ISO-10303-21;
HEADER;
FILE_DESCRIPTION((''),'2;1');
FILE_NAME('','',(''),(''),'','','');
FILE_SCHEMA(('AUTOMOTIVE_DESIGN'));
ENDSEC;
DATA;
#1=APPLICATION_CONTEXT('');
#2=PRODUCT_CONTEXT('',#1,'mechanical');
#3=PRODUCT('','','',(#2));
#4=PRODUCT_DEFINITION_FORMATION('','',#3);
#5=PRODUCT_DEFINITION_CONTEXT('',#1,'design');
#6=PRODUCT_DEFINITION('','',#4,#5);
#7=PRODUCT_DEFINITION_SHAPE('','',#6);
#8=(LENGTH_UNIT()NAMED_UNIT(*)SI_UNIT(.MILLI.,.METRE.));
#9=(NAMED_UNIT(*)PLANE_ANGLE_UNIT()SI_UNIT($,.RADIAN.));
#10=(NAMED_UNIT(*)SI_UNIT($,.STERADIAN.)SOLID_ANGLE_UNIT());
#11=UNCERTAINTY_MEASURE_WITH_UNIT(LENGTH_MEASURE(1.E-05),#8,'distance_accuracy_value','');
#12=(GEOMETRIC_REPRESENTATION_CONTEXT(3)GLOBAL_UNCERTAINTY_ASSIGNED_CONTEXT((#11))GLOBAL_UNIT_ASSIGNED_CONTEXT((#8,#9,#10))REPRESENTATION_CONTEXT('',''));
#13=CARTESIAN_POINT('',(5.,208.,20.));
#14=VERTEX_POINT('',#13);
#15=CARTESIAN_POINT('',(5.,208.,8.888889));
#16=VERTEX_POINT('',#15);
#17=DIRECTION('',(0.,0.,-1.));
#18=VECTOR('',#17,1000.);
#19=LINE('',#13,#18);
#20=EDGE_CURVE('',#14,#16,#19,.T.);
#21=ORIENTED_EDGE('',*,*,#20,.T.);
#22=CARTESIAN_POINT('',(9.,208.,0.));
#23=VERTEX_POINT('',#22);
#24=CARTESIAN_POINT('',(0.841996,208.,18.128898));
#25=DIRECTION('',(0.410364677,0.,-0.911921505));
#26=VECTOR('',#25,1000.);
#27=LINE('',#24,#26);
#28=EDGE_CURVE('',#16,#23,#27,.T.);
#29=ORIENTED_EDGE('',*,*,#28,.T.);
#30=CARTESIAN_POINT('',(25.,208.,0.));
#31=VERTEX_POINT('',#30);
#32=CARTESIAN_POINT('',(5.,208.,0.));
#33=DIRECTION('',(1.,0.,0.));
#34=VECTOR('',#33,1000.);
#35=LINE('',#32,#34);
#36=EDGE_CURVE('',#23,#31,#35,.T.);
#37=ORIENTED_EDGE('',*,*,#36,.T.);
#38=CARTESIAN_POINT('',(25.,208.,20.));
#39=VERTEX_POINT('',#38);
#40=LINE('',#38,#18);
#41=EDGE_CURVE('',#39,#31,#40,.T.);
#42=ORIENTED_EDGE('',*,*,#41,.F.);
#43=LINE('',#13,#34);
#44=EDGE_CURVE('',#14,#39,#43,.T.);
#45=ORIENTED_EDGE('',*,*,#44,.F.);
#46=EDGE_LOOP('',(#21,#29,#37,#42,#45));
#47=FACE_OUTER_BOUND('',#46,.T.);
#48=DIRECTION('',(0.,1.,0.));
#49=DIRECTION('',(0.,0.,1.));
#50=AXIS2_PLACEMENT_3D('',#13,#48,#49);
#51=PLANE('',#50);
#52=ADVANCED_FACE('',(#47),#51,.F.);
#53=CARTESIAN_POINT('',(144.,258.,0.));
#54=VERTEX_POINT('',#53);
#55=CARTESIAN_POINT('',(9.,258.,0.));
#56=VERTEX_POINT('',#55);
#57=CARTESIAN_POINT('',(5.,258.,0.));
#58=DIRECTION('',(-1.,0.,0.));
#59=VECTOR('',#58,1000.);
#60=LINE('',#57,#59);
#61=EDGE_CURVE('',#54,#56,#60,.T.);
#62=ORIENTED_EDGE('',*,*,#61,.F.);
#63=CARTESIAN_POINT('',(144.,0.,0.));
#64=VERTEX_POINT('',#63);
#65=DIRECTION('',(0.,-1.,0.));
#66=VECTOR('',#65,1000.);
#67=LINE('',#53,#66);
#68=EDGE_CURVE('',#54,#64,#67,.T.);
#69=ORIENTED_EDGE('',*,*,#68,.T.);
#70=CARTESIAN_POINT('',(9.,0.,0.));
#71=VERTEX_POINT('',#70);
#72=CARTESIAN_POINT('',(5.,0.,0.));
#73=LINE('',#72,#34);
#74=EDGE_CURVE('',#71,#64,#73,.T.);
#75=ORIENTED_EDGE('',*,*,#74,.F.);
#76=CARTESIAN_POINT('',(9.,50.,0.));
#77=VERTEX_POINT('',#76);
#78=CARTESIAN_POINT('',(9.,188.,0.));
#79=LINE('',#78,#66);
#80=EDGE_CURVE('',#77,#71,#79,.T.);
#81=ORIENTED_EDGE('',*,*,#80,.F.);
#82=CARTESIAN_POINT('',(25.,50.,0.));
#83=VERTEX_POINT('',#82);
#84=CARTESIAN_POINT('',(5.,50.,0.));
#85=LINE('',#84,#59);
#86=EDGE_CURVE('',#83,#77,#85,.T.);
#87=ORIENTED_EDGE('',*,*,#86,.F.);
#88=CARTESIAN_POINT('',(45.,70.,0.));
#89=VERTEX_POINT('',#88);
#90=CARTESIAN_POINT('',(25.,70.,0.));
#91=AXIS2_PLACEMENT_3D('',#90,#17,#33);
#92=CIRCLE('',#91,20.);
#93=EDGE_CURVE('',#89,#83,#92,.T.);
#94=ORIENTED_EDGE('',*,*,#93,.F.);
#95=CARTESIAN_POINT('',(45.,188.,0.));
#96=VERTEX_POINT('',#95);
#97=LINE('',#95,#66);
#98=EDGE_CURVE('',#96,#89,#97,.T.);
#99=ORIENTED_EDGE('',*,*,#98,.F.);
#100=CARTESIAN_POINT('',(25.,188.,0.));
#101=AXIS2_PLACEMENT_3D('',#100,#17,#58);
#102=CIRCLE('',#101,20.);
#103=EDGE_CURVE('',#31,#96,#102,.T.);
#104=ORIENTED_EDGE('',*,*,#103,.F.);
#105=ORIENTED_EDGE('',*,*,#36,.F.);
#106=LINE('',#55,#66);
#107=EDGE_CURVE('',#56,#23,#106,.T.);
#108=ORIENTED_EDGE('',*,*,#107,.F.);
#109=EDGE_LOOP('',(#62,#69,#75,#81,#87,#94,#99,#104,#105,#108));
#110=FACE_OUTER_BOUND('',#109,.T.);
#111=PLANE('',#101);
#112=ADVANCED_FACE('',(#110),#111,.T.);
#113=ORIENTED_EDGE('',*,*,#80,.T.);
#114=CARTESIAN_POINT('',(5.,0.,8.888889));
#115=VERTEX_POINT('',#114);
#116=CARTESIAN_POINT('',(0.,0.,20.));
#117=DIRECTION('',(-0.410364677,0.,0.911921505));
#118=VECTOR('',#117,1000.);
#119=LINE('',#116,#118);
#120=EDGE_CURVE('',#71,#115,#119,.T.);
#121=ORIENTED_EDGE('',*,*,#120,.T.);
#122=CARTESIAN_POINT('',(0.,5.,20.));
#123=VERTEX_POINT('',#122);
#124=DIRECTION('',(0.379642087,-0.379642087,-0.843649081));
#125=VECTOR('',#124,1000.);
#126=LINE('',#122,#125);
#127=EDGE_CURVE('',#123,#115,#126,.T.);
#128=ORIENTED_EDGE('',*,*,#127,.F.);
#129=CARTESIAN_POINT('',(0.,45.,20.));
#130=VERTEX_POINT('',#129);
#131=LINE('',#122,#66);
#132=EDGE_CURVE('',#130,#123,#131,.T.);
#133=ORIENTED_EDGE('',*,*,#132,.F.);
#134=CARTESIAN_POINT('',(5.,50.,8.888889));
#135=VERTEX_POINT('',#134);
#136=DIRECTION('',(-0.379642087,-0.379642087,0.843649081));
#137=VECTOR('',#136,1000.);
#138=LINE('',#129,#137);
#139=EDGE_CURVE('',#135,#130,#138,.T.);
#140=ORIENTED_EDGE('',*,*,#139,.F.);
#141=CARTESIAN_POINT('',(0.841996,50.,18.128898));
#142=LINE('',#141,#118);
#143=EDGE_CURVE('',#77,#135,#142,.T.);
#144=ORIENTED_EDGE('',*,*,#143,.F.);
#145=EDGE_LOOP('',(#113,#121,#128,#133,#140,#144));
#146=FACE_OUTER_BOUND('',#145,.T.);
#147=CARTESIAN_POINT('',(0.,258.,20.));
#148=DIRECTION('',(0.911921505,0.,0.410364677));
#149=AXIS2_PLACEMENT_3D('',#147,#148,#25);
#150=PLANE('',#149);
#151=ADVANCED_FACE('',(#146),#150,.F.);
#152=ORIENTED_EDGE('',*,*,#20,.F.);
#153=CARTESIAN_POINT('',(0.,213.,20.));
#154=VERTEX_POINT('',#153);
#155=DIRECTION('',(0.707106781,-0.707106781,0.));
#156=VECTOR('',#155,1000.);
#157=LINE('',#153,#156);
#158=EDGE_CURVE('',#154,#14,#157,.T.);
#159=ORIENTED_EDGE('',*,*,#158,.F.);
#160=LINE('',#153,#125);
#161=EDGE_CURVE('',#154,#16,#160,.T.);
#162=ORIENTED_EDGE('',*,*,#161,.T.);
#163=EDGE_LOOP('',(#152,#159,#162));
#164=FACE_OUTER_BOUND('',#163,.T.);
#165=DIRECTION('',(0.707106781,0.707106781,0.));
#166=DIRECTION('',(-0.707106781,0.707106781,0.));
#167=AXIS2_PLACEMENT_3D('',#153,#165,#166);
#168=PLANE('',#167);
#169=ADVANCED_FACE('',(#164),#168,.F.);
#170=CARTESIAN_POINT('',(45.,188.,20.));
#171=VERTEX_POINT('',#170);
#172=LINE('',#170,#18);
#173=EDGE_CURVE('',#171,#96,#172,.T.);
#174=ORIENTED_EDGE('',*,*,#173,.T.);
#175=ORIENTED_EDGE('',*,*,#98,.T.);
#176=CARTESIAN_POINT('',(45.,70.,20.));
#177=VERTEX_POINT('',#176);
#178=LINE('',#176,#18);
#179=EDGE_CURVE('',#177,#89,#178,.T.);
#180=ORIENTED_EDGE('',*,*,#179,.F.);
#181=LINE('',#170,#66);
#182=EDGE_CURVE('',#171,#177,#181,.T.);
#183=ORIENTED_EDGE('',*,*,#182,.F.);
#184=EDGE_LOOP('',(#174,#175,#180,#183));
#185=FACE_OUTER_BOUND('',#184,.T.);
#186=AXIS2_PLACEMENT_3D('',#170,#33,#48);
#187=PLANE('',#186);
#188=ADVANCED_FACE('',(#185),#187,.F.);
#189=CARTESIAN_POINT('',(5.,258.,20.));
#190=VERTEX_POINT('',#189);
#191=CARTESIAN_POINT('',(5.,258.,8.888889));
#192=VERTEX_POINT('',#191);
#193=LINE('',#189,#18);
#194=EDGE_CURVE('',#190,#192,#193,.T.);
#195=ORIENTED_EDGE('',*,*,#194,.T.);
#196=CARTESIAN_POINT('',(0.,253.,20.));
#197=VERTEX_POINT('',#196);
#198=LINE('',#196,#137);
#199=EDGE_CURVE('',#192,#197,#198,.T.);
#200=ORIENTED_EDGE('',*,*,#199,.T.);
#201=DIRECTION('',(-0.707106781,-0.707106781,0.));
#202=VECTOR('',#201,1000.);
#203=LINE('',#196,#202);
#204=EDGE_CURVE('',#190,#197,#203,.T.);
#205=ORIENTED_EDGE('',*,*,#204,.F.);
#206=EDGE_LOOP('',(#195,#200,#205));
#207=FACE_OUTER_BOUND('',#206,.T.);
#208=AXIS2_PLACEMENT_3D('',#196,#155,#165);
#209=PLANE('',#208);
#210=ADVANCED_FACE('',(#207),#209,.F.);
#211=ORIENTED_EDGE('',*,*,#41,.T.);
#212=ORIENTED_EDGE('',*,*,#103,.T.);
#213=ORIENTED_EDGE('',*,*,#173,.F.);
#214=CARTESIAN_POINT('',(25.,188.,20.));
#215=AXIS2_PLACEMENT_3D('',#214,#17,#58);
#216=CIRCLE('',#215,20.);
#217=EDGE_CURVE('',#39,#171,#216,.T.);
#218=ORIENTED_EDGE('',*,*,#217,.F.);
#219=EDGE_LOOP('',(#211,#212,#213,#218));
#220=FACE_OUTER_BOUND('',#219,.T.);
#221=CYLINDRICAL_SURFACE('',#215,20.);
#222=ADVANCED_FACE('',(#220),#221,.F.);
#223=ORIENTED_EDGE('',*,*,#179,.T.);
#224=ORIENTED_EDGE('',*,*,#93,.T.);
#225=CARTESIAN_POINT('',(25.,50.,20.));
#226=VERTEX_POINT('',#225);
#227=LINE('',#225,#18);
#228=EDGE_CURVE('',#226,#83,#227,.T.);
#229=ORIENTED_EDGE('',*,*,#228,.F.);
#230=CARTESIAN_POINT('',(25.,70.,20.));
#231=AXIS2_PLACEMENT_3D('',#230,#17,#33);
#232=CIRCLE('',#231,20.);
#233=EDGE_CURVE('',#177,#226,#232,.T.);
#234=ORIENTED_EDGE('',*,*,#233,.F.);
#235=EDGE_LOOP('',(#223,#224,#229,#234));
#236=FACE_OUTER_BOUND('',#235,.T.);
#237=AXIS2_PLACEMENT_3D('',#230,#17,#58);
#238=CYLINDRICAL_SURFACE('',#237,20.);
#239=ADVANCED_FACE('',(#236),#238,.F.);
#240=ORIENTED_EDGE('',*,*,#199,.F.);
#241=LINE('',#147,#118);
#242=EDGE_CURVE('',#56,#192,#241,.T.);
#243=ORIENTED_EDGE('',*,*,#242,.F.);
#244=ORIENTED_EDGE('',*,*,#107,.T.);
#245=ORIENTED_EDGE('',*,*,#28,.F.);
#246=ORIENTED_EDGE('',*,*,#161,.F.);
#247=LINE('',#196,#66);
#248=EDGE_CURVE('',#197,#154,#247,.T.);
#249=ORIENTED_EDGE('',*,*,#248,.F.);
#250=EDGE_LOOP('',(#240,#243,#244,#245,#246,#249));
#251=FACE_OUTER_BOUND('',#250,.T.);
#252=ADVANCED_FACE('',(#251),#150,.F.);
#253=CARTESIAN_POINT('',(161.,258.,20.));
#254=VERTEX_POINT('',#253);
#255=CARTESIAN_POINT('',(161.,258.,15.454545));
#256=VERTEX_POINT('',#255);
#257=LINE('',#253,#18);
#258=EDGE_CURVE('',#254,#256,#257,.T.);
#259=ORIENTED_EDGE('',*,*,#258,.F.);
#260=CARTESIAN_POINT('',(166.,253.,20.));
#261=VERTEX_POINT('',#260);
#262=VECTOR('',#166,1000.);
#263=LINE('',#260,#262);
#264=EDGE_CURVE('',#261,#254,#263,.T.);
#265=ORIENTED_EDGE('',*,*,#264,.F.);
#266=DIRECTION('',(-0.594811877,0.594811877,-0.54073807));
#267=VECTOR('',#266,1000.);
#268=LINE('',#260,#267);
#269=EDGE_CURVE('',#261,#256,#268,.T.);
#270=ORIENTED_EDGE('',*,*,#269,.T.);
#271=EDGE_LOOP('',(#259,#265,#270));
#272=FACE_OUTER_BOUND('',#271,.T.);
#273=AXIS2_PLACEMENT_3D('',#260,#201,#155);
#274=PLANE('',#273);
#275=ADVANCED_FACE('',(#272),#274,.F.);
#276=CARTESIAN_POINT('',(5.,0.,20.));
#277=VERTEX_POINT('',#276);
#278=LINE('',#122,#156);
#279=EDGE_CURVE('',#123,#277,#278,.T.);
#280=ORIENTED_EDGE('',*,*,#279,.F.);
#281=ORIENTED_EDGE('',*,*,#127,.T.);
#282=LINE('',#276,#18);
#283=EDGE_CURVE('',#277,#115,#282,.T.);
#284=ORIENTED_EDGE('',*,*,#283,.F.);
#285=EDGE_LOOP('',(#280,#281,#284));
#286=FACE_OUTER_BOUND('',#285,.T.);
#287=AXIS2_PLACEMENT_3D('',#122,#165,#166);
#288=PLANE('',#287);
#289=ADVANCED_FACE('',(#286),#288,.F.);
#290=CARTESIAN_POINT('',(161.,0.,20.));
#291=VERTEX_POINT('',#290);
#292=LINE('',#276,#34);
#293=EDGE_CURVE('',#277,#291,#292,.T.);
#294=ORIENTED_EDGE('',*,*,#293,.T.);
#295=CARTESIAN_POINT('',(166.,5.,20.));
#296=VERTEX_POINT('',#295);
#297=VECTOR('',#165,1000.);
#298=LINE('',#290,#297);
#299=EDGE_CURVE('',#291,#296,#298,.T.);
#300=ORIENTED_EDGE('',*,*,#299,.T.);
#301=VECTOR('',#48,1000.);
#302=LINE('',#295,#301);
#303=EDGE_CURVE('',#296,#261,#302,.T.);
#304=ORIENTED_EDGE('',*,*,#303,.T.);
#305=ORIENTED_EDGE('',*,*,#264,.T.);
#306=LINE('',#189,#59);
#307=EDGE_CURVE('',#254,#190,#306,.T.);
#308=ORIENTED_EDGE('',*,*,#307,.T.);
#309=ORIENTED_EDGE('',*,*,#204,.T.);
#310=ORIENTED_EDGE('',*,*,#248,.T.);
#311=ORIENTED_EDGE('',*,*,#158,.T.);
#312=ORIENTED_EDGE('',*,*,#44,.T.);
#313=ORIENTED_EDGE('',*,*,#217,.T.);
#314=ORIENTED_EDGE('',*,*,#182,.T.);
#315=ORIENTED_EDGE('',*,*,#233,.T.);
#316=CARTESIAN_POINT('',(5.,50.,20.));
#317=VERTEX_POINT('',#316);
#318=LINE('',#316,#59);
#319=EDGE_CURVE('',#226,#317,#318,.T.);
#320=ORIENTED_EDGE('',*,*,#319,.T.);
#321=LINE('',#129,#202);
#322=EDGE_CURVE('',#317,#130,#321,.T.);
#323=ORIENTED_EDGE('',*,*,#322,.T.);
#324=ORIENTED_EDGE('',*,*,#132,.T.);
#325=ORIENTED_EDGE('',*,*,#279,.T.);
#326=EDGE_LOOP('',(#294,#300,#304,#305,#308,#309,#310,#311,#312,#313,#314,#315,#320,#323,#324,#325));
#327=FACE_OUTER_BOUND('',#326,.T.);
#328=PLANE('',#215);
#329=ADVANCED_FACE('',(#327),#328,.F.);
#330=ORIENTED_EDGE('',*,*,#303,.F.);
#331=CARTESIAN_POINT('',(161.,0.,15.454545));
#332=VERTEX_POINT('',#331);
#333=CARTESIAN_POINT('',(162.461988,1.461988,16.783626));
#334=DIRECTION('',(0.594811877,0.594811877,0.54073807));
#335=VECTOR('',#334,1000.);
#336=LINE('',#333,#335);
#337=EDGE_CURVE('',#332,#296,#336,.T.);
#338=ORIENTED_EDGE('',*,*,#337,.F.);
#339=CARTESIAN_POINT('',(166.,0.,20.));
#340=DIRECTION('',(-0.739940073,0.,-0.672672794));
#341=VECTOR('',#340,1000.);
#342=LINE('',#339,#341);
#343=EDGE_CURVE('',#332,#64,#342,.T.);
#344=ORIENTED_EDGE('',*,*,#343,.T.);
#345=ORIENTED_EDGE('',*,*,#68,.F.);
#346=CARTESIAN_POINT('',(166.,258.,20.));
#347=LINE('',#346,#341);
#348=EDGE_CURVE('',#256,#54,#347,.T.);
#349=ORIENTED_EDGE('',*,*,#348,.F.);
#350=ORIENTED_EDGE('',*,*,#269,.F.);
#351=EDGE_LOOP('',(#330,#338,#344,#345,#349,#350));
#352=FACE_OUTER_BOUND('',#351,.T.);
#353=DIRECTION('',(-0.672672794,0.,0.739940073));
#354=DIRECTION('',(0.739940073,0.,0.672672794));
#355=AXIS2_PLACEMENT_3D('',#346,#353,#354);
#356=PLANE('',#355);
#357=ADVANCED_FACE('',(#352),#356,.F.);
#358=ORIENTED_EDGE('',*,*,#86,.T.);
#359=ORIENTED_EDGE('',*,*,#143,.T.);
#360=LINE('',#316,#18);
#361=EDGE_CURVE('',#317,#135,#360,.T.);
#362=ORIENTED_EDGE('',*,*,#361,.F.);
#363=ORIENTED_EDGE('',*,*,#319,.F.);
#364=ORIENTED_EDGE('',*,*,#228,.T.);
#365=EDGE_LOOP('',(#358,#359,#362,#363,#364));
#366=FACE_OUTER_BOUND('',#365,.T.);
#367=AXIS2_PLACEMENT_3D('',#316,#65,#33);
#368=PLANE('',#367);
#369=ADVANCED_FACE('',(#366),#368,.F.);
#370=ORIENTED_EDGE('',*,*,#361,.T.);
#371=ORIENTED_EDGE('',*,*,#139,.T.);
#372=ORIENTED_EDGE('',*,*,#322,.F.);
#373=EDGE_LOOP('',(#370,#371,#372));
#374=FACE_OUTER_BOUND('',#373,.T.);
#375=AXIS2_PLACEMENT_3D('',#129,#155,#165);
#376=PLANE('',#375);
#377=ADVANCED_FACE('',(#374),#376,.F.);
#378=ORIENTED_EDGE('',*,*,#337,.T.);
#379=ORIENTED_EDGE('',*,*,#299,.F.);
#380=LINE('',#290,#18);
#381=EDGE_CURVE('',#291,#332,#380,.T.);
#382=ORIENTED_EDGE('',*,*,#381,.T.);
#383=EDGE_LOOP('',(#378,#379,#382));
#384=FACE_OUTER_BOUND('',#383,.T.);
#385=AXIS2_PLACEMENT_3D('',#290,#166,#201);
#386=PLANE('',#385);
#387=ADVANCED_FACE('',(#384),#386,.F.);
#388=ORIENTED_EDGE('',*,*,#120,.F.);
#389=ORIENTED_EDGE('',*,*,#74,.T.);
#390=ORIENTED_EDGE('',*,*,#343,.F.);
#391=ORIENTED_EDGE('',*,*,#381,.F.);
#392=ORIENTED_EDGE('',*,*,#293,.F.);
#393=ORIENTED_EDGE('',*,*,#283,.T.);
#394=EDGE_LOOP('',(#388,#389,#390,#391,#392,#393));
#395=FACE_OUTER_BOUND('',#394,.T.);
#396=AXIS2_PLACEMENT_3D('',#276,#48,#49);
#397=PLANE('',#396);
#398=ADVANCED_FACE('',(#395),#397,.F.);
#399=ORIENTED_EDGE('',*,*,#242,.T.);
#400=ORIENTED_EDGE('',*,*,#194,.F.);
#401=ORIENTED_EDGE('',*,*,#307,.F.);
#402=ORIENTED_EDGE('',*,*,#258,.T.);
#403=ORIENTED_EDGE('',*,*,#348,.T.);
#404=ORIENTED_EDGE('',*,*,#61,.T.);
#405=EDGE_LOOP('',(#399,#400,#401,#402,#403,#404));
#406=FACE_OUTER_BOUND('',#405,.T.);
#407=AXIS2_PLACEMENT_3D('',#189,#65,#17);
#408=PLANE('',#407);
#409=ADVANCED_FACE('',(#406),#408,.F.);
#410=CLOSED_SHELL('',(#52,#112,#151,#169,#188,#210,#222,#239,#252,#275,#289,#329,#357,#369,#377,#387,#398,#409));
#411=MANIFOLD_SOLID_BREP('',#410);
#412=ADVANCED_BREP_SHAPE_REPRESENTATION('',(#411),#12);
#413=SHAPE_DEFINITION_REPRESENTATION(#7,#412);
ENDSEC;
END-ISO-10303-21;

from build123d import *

# Parameters (mm, degrees)
BOSS_EXTRUDE1_DEPTH = 20
CUT_EXTRUDE1_DEPTH  = 308.44105126


with BuildPart() as part:
    # Sketch1 → Boss-Extrude1 (new body)
    with BuildSketch(Plane.XY):
        with BuildLine():
            Line((45, 188), (45, 70))
            ThreePointArc((45, 70), (39.142135624, 55.857864376), (25, 50))
            Line((25, 50), (5, 50))
            Line((5, 50), (0, 45))
            Line((0, 45), (0, 5))
            Line((0, 5), (5, 0))
            Line((5, 0), (161, 0))
            Line((161, 0), (166, 5))
            Line((166, 5), (166, 253))
            Line((166, 253), (161, 258))
            Line((161, 258), (5, 258))
            Line((5, 258), (0, 253))
            Line((0, 253), (0, 213))
            Line((0, 213), (5, 208))
            Line((5, 208), (25, 208))
            ThreePointArc((25, 208), (39.142135624, 202.142135624), (45, 188))
        make_face()
    extrude(amount=BOSS_EXTRUDE1_DEPTH)

    # Sketch2 → Cut-Extrude1 (cut, through all)
    with BuildSketch(Plane.XZ):
        Polygon((0, 20), (0, 0), (9, 0), align=None)
        Polygon((166, 20), (166, 0), (144, 0), align=None)
    extrude(amount=-CUT_EXTRUDE1_DEPTH, mode=Mode.SUBTRACT)


solid = part.part
